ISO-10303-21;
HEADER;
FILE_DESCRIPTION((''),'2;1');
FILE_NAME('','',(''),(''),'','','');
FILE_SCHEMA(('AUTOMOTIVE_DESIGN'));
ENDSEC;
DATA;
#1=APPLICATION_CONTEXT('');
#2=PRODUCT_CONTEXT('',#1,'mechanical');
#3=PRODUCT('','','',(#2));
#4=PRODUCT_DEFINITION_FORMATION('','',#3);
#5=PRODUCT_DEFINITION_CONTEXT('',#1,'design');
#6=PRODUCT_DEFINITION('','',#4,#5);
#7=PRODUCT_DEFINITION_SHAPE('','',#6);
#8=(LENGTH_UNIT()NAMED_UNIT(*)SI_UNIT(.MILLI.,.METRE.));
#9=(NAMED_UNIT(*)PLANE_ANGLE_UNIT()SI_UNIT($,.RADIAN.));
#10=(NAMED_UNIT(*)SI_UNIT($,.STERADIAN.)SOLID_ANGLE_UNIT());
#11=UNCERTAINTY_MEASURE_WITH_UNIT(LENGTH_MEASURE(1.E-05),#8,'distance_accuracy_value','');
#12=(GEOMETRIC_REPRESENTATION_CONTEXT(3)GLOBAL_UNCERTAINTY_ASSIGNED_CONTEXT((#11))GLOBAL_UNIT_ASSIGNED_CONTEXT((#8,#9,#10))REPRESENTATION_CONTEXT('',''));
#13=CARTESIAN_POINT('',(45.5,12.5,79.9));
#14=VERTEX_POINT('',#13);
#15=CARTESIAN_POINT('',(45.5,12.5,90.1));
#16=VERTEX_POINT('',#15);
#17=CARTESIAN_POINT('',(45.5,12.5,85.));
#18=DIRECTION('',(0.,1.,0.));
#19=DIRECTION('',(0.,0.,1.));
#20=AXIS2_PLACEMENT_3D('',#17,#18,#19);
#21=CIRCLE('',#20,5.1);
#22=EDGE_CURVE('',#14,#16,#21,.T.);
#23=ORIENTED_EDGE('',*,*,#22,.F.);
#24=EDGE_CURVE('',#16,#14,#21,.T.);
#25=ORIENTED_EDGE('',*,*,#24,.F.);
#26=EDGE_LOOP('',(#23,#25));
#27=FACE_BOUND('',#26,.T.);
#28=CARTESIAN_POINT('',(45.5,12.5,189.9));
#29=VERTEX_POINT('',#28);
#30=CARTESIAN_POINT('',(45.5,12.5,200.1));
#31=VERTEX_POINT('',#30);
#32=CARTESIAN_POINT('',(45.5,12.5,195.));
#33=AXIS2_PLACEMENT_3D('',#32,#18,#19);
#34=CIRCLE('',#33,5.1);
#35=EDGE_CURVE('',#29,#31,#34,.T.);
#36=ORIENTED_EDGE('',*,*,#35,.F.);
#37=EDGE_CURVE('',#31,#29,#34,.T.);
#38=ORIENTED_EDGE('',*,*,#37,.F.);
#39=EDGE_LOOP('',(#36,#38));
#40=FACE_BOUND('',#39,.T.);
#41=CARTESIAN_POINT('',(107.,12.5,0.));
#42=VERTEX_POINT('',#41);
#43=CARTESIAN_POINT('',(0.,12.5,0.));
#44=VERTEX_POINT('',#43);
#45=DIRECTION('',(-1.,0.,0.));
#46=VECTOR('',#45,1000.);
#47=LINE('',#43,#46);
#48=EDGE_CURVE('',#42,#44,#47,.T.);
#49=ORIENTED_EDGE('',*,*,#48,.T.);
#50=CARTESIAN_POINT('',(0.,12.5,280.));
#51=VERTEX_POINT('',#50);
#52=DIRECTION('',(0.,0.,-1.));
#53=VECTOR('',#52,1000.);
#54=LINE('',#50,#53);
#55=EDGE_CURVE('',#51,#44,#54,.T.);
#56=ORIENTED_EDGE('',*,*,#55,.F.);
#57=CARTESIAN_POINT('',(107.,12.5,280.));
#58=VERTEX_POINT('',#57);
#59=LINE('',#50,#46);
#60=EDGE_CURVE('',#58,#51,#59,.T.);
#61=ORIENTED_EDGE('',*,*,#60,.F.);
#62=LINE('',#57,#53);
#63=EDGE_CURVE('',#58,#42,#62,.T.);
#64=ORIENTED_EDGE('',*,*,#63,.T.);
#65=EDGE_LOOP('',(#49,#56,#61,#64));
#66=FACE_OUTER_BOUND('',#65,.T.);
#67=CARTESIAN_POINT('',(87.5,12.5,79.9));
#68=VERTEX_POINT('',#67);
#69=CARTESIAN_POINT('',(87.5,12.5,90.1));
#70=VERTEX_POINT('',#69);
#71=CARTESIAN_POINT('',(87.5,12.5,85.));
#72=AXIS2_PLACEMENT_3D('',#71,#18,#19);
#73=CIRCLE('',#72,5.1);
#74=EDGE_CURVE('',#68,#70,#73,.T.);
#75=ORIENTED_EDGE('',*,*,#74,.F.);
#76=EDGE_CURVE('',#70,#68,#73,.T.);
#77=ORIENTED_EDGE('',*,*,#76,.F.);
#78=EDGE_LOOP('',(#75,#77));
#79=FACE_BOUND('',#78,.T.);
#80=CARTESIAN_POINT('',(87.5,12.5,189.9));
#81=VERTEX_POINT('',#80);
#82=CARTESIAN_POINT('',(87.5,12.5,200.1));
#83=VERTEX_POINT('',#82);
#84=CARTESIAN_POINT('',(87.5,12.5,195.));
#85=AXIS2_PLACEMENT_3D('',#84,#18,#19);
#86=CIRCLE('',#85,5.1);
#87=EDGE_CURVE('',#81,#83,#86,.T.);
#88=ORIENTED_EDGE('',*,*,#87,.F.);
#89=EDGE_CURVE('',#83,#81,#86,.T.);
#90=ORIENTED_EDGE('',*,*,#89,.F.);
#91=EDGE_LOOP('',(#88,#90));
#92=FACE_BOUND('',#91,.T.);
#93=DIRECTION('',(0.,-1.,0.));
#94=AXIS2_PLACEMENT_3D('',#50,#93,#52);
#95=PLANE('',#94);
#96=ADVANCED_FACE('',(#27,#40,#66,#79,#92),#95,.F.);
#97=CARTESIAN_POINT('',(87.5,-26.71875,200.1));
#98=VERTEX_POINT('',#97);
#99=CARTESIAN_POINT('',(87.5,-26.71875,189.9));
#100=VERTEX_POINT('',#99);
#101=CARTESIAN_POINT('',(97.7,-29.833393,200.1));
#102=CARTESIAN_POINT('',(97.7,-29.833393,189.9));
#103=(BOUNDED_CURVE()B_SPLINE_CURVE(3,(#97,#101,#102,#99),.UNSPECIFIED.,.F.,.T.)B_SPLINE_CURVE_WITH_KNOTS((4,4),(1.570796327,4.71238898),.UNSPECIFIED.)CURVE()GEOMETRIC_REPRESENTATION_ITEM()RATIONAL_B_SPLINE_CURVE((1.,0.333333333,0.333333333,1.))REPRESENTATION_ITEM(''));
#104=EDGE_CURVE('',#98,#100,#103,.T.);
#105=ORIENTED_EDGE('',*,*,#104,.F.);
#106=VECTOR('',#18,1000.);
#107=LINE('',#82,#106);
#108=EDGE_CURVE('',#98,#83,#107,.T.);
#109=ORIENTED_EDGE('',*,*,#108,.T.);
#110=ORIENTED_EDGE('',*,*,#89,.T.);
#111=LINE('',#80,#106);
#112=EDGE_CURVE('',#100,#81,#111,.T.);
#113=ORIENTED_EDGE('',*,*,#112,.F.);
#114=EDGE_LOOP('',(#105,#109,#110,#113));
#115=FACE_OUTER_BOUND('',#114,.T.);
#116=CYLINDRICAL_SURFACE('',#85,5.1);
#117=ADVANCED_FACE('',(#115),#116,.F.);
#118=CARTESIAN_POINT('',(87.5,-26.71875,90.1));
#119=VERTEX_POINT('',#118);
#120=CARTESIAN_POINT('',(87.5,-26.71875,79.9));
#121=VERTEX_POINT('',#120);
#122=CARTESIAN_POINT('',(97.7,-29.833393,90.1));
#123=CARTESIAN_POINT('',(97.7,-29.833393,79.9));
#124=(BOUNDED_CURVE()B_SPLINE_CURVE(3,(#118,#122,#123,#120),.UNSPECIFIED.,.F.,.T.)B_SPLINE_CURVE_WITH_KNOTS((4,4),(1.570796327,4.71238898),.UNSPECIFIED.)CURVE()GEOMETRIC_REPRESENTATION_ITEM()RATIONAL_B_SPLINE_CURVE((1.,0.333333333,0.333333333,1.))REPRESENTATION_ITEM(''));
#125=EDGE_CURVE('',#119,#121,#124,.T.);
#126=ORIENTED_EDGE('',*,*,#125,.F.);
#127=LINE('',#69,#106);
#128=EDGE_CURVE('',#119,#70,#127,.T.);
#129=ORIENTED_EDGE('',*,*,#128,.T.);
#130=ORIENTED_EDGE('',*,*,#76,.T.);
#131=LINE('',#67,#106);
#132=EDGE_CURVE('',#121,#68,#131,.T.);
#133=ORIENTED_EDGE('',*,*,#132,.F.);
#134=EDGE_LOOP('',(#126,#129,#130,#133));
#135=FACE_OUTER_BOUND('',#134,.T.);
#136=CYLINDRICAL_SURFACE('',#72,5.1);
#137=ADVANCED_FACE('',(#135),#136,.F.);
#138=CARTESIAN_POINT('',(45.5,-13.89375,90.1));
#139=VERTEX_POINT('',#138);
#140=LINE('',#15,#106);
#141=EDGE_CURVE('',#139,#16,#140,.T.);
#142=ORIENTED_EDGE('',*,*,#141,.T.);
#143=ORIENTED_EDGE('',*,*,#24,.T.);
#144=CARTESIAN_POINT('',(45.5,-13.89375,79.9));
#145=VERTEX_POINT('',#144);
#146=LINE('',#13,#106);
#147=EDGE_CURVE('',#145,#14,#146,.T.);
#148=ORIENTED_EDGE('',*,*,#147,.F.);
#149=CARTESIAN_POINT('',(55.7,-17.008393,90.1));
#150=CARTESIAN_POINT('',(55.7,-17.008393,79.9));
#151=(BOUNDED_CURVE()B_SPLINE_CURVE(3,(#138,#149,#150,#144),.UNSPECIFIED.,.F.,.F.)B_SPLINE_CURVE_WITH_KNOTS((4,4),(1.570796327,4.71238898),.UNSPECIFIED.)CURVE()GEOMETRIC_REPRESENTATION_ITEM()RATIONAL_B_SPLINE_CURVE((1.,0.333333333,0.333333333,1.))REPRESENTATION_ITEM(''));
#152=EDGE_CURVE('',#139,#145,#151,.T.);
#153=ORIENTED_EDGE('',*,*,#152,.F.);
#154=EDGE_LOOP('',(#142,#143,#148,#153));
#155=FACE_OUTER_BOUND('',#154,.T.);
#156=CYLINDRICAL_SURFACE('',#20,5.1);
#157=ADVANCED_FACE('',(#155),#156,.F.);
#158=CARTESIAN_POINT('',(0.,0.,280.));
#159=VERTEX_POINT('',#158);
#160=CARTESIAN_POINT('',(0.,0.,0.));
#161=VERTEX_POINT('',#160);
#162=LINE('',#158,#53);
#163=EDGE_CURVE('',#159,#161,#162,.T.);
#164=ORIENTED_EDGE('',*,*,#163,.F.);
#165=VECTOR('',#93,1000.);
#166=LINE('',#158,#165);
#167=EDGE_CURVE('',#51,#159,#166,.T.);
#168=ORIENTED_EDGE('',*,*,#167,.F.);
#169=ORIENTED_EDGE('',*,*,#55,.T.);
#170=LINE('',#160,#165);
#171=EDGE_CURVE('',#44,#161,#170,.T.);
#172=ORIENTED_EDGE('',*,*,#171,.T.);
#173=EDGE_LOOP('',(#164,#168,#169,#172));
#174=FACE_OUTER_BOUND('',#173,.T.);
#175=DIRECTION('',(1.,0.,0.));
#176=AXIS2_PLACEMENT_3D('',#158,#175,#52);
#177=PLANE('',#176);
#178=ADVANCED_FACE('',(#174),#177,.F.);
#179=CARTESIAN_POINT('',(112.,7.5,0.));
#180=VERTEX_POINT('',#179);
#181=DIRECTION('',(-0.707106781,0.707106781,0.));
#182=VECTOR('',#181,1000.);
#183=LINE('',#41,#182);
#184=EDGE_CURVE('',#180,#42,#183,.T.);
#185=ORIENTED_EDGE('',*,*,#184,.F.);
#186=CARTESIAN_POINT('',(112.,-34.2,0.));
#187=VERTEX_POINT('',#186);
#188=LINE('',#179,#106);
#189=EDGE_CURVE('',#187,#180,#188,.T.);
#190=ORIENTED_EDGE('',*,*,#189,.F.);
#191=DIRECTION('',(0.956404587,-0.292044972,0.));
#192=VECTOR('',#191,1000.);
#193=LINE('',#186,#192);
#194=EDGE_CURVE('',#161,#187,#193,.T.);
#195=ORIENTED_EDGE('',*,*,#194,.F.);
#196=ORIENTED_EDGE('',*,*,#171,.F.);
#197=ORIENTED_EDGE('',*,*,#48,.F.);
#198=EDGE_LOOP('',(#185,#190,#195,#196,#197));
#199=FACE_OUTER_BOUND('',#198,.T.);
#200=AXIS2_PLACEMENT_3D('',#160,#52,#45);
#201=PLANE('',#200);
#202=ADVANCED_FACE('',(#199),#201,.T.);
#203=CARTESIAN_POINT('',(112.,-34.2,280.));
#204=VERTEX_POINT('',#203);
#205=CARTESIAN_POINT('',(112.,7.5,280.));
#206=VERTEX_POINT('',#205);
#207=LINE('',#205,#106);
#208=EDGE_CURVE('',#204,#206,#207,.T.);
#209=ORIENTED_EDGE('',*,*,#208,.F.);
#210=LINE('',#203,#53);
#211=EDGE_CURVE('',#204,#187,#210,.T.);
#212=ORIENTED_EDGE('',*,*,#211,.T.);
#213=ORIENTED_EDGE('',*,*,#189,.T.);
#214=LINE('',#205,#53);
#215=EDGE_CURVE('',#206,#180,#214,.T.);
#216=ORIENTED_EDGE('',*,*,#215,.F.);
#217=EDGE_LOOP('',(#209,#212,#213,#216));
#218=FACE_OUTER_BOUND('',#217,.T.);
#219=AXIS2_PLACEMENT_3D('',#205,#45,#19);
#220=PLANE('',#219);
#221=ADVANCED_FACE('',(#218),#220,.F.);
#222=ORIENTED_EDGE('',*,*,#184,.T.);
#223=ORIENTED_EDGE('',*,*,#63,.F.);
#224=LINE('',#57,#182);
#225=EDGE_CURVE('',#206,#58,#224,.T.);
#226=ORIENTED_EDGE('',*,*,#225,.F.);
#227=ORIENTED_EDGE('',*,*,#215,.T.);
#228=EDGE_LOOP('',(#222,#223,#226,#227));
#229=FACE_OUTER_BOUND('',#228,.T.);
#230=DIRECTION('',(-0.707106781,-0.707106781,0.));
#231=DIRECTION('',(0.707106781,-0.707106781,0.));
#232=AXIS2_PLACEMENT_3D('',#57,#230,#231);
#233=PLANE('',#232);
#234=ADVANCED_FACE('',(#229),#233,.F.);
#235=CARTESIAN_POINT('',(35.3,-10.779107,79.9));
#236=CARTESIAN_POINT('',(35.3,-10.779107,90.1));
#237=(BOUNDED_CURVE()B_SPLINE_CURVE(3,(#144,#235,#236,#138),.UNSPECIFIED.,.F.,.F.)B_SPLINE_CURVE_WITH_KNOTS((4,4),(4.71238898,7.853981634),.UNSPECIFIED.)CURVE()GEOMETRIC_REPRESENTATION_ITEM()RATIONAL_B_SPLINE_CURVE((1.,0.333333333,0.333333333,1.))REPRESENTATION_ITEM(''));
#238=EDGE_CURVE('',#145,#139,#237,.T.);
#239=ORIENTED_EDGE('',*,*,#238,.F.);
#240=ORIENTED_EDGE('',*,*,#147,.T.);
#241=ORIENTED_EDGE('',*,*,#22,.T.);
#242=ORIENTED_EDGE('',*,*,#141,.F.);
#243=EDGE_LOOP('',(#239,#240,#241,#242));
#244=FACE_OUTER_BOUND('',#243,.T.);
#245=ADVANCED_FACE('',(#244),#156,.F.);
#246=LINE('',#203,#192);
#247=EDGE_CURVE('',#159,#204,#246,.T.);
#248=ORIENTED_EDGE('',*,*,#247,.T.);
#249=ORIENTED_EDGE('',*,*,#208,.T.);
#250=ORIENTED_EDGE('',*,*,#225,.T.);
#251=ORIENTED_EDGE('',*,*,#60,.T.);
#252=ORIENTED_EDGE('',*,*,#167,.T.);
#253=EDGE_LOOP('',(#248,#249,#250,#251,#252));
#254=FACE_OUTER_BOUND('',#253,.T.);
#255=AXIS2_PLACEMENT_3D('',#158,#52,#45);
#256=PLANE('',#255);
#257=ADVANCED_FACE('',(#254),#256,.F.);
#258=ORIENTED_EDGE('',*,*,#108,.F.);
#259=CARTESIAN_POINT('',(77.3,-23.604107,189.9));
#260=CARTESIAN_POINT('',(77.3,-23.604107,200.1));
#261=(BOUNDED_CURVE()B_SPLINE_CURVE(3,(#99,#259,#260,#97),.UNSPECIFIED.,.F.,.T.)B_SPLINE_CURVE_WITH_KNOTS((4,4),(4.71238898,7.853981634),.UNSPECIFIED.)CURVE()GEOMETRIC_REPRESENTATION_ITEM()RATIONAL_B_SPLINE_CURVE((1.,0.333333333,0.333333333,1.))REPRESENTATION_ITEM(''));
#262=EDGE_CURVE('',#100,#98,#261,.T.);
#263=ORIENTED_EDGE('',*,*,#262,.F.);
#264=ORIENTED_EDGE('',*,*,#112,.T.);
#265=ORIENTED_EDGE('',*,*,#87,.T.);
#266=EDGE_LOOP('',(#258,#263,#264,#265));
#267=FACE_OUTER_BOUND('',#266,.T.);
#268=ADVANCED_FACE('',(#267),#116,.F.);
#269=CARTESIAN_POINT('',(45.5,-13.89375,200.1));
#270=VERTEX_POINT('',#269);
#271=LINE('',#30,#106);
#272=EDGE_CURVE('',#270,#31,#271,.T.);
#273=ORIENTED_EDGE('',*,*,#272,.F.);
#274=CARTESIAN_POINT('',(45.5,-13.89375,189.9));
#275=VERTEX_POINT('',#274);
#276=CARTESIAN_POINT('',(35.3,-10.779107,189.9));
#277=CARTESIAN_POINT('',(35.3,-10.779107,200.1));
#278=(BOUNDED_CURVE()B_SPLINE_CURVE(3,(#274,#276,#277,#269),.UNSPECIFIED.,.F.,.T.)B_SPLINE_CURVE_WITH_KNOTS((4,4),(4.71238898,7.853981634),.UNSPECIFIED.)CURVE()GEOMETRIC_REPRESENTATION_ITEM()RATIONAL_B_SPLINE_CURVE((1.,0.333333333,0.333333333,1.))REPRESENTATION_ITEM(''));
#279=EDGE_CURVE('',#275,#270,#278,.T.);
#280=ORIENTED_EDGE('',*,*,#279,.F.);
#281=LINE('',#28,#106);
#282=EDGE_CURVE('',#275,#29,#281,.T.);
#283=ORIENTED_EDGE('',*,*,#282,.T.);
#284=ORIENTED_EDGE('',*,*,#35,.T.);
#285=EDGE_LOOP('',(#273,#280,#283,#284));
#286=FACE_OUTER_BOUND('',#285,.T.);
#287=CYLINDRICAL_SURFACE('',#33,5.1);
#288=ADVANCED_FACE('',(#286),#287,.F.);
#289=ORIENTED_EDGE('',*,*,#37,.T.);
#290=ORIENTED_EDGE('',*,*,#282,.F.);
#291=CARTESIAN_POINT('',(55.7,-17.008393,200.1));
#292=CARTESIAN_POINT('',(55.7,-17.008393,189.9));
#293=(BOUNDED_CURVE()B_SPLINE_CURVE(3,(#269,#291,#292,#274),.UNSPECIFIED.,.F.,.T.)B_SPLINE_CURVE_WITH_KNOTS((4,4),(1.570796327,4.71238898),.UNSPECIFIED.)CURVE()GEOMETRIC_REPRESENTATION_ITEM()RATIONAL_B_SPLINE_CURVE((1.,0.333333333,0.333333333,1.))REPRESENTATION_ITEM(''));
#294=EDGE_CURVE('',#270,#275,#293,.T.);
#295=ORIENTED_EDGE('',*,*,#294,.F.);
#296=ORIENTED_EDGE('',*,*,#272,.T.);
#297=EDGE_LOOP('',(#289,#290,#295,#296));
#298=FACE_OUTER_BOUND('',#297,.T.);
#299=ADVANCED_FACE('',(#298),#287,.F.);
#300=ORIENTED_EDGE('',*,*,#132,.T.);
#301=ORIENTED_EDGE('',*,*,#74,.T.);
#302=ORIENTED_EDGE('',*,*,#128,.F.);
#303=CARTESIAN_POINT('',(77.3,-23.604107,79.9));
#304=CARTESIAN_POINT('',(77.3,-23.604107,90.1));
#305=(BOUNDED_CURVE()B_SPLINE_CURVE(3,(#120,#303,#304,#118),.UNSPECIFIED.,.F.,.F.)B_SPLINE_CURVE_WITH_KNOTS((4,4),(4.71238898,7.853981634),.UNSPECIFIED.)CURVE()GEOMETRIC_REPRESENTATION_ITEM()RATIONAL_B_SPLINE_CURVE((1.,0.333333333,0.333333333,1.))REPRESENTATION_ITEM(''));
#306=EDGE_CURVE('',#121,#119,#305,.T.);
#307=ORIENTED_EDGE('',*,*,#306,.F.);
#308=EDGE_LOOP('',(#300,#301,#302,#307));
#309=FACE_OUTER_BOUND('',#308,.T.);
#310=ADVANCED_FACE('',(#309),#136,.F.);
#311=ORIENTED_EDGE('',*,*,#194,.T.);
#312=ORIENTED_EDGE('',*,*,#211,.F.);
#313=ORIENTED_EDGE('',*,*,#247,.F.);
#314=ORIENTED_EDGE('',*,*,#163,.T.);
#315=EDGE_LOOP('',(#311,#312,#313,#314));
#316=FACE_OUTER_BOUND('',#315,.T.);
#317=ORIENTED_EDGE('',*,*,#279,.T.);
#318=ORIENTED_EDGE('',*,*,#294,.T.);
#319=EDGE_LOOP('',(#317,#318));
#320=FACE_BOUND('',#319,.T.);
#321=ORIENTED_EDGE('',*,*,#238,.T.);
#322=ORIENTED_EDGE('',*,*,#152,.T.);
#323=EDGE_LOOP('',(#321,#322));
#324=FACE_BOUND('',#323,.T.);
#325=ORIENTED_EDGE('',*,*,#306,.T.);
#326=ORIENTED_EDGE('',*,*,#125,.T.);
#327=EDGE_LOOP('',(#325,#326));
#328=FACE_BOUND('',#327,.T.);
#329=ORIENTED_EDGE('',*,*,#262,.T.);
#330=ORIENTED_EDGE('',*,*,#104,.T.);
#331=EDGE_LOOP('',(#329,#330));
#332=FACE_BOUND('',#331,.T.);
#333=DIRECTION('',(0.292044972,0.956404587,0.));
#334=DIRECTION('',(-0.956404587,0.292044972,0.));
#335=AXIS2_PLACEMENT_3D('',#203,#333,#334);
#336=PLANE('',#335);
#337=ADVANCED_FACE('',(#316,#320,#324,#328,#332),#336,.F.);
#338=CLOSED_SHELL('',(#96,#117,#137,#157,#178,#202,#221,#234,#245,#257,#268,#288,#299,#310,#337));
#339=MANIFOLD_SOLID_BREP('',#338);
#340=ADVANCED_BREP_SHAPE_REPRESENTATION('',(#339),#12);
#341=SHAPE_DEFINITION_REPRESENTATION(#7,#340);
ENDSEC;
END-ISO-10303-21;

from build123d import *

# Parameters (mm, degrees)
BOSS_EXTRUDE1_DEPTH = 280
M12_TAPPED_HOLE1_D  = 10.2


with BuildPart() as part:
    # Sketch1 → Boss-Extrude1 (new body)
    with BuildSketch(Plane.XY):
        Polygon((0, 0), (0, 12.5), (107, 12.5), (112, 7.5), (112, -34.2), align=None)
    extrude(amount=BOSS_EXTRUDE1_DEPTH)

    # M12 Tapped Hole1 (through all)
    with Locations(Plane(origin=(0, 12.5, 0), x_dir=(-1, 0, 0), z_dir=(0, 1, 0))):
        with Locations((-45.5, 195), (-45.5, 85), (-87.5, 85), (-87.5, 195)):
            Hole(M12_TAPPED_HOLE1_D / 2)


solid = part.part
